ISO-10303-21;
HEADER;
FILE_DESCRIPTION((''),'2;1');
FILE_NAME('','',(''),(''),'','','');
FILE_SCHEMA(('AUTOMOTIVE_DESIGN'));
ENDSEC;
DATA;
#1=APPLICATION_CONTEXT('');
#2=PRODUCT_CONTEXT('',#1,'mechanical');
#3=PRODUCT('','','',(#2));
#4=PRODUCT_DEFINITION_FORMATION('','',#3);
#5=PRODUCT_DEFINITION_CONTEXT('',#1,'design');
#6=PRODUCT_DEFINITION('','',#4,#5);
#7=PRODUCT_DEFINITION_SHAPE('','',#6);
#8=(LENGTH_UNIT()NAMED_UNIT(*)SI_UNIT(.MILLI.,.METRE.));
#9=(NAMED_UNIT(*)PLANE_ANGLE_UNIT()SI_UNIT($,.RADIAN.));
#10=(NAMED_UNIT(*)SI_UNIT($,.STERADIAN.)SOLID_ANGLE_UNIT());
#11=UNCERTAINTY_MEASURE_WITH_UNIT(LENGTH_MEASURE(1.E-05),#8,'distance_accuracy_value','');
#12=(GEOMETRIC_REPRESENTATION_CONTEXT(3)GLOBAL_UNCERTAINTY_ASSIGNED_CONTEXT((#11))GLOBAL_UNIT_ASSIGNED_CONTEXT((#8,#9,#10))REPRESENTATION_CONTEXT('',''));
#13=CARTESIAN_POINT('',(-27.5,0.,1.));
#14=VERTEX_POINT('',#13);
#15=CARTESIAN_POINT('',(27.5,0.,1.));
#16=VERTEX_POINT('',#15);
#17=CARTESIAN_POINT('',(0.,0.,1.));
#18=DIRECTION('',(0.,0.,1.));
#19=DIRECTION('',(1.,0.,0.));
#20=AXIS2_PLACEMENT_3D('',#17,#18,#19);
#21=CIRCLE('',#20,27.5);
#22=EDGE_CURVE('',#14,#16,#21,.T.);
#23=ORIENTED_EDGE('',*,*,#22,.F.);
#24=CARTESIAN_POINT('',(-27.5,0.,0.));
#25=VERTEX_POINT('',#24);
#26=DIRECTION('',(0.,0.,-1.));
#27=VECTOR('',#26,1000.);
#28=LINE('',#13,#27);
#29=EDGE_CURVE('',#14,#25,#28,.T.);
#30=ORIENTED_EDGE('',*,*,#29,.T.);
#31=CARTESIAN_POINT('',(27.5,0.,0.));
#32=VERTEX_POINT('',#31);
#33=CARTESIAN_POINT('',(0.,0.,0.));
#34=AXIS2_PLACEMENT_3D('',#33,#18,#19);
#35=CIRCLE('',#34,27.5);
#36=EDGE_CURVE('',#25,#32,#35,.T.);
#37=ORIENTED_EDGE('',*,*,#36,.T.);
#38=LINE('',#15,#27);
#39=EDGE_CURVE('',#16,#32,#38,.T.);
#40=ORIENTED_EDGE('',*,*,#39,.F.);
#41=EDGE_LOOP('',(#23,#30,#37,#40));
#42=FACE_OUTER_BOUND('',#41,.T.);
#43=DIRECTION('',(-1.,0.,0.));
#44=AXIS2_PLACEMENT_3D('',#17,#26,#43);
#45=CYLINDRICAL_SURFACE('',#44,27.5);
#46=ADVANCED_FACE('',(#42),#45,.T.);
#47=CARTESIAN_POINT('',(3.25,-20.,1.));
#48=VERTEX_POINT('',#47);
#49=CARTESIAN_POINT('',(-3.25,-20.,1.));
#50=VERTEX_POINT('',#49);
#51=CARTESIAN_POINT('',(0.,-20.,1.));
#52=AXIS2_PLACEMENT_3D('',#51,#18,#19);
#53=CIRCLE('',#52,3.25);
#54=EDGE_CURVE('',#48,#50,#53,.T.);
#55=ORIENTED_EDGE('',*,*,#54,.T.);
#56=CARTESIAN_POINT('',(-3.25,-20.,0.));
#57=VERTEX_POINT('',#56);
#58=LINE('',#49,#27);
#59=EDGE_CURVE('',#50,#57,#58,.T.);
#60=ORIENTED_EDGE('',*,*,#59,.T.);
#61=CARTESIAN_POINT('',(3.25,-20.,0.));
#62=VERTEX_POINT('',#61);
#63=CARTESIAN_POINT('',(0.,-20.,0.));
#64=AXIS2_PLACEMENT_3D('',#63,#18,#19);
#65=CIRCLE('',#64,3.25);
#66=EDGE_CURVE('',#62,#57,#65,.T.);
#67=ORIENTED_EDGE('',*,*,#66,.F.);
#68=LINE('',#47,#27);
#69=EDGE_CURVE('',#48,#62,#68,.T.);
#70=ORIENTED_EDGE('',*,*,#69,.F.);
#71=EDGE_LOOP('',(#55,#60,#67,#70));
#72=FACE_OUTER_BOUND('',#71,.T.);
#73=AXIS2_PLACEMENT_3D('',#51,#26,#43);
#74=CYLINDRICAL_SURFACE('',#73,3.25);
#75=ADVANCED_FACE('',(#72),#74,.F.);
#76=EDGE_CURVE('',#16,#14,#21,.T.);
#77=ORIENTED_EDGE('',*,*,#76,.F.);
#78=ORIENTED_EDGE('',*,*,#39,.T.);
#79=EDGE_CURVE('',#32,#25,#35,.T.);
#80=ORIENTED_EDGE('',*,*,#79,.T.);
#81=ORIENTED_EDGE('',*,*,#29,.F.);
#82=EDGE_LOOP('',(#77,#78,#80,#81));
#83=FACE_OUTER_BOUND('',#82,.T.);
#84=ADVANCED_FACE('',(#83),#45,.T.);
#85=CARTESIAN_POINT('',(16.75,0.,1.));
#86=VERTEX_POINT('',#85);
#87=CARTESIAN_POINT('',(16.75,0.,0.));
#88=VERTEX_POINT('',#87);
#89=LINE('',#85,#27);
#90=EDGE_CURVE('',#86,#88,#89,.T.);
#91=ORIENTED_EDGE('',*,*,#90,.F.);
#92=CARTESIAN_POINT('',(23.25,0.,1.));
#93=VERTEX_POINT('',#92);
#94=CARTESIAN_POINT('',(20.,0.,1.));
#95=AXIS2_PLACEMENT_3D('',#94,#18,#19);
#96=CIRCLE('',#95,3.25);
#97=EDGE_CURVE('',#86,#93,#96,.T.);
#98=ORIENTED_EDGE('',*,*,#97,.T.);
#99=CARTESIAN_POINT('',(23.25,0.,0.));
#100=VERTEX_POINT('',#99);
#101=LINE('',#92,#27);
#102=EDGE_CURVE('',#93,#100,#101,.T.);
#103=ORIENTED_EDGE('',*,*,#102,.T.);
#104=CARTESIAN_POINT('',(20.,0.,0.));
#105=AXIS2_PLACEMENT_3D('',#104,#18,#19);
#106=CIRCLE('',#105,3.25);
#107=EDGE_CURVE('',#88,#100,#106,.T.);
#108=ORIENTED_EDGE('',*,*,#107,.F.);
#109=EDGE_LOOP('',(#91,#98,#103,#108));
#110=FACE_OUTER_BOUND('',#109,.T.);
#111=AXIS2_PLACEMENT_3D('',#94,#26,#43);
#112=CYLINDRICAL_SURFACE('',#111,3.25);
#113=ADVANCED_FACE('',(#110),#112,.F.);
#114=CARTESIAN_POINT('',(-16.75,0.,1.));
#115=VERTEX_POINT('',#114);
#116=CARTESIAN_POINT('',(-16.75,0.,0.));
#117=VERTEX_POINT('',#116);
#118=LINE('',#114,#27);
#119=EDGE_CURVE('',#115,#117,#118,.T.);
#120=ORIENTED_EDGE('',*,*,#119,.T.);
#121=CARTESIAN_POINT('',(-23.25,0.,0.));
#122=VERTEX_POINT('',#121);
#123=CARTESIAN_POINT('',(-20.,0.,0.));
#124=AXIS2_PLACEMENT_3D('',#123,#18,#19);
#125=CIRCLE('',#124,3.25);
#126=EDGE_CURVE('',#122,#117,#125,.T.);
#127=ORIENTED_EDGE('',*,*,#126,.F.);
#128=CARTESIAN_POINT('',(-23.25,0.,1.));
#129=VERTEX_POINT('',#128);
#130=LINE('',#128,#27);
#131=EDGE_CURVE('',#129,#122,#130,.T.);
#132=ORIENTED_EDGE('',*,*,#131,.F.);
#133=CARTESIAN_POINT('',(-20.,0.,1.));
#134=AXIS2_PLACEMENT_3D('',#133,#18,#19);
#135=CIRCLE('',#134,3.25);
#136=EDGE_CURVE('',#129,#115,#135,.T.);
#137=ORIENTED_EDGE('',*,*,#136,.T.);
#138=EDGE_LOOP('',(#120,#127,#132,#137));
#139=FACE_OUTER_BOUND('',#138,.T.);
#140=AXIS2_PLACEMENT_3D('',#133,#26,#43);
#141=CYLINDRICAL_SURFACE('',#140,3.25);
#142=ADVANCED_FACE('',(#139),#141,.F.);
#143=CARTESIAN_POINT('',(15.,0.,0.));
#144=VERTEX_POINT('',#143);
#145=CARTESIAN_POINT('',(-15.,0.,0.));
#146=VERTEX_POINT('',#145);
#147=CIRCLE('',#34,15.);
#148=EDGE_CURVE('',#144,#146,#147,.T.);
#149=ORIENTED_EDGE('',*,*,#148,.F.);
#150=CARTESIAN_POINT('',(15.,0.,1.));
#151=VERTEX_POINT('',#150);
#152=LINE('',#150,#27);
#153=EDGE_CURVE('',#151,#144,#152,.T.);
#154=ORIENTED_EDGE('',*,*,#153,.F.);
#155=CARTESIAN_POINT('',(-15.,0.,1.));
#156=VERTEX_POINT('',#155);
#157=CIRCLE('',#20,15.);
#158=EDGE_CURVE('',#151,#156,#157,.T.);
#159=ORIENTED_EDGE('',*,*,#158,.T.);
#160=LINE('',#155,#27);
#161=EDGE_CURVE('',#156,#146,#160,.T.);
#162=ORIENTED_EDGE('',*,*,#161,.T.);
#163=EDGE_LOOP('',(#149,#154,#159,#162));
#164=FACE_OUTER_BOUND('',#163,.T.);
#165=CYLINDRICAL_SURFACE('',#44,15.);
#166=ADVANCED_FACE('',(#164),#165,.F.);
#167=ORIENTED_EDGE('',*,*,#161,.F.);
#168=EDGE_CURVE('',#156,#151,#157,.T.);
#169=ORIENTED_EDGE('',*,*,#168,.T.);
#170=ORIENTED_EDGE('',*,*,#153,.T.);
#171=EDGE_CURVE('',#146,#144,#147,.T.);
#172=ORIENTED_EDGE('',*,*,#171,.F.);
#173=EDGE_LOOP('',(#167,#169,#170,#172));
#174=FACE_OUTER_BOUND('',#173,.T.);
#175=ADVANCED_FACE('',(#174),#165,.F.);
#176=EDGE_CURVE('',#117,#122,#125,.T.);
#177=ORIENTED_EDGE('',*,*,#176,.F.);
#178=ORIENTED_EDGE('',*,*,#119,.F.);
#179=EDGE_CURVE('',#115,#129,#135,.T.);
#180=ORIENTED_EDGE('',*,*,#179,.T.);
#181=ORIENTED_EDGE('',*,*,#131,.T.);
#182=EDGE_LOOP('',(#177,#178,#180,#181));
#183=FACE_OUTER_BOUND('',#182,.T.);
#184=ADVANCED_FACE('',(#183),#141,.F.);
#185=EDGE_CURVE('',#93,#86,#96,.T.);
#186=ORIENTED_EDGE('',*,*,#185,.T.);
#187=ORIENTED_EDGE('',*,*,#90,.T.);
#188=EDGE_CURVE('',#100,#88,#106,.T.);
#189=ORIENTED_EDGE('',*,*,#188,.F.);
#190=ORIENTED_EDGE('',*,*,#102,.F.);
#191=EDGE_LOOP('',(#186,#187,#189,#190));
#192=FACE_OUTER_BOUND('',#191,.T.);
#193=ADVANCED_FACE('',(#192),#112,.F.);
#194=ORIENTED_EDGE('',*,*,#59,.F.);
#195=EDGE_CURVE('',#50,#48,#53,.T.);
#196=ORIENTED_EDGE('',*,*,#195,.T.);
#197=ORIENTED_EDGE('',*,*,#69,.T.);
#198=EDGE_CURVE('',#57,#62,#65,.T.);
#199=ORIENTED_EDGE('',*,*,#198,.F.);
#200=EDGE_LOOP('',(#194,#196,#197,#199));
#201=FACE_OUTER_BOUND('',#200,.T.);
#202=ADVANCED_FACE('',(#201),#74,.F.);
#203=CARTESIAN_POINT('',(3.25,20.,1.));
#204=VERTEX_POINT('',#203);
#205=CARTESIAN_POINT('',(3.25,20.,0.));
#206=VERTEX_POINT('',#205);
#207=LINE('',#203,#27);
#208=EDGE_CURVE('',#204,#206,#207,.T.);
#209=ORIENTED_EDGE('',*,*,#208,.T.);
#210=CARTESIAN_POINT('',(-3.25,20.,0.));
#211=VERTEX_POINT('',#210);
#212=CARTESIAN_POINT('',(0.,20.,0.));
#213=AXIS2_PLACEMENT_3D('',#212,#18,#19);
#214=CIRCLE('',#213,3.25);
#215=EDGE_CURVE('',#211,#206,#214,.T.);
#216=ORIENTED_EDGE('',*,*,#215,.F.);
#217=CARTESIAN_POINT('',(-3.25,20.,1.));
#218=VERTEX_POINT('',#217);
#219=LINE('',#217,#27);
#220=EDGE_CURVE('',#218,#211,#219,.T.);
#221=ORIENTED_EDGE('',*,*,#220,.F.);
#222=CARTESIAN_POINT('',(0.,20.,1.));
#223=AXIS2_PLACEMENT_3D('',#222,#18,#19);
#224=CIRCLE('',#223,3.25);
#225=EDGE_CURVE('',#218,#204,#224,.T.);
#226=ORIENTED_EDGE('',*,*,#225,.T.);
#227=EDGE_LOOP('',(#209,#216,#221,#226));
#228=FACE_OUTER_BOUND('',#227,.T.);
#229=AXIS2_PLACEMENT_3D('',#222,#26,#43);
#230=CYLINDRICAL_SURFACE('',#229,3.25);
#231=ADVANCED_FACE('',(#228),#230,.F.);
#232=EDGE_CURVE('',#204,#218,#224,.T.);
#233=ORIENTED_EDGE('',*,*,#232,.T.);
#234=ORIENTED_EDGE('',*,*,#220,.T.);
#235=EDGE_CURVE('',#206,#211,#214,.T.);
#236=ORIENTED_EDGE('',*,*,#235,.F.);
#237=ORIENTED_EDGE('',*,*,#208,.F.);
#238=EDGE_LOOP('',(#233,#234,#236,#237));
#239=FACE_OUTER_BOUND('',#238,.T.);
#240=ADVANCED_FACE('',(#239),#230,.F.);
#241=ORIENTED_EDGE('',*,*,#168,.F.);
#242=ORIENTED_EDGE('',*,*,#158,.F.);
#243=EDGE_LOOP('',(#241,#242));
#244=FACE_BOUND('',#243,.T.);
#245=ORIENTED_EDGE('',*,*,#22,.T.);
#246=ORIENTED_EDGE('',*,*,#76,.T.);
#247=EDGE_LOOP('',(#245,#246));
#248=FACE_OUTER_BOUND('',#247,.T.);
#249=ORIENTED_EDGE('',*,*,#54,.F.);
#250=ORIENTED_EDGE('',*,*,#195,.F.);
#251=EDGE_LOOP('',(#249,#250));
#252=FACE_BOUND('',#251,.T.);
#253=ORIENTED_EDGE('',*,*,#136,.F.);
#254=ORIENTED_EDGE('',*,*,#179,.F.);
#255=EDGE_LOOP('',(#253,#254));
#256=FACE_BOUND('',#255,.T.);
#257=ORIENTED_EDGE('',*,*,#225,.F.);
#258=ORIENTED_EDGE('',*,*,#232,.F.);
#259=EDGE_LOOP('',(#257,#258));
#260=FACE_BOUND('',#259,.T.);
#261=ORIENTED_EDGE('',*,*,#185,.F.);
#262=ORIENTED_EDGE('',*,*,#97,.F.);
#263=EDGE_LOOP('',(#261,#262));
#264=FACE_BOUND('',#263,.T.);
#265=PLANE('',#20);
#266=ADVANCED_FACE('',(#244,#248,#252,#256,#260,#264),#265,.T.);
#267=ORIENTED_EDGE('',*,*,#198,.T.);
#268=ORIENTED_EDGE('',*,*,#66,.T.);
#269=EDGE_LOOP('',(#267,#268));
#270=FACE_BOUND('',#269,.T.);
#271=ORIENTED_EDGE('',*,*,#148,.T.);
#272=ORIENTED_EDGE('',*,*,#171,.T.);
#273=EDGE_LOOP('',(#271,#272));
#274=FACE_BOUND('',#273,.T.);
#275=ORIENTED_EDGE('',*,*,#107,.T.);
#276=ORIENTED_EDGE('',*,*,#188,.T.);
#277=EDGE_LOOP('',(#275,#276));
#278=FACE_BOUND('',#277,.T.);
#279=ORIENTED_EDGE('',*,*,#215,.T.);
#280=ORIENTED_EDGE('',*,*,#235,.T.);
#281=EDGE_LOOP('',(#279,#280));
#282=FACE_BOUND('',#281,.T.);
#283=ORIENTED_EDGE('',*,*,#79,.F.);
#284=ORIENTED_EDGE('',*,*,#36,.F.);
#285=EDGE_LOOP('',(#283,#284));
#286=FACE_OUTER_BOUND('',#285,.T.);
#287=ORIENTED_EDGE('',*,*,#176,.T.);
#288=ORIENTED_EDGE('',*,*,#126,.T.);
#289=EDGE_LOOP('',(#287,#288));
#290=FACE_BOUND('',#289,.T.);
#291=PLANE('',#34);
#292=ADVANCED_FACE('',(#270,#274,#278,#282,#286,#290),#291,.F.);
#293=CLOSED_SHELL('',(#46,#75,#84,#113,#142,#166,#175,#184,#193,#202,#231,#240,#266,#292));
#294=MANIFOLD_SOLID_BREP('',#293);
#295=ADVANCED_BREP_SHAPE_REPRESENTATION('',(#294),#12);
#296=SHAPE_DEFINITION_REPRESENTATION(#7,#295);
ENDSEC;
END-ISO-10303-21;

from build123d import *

# Parameters (mm, degrees)
SKETCH1_R           = 27.5
SKETCH1_R_2         = 15
SKETCH1_R_3         = 3.25
BOSS_EXTRUDE1_DEPTH = 1


with BuildPart() as part:
    # Sketch1 → Boss-Extrude1 (new body)
    with BuildSketch(Plane.XY):
        Circle(SKETCH1_R)
        Circle(SKETCH1_R_2, mode=Mode.SUBTRACT)
        with Locations((0, 20)):
            Circle(SKETCH1_R_3, mode=Mode.SUBTRACT)
        with Locations((20, 0)):
            Circle(SKETCH1_R_3, mode=Mode.SUBTRACT)
        with Locations((0, -20)):
            Circle(SKETCH1_R_3, mode=Mode.SUBTRACT)
        with Locations((-20, 0)):
            Circle(SKETCH1_R_3, mode=Mode.SUBTRACT)
    extrude(amount=BOSS_EXTRUDE1_DEPTH)


solid = part.part
